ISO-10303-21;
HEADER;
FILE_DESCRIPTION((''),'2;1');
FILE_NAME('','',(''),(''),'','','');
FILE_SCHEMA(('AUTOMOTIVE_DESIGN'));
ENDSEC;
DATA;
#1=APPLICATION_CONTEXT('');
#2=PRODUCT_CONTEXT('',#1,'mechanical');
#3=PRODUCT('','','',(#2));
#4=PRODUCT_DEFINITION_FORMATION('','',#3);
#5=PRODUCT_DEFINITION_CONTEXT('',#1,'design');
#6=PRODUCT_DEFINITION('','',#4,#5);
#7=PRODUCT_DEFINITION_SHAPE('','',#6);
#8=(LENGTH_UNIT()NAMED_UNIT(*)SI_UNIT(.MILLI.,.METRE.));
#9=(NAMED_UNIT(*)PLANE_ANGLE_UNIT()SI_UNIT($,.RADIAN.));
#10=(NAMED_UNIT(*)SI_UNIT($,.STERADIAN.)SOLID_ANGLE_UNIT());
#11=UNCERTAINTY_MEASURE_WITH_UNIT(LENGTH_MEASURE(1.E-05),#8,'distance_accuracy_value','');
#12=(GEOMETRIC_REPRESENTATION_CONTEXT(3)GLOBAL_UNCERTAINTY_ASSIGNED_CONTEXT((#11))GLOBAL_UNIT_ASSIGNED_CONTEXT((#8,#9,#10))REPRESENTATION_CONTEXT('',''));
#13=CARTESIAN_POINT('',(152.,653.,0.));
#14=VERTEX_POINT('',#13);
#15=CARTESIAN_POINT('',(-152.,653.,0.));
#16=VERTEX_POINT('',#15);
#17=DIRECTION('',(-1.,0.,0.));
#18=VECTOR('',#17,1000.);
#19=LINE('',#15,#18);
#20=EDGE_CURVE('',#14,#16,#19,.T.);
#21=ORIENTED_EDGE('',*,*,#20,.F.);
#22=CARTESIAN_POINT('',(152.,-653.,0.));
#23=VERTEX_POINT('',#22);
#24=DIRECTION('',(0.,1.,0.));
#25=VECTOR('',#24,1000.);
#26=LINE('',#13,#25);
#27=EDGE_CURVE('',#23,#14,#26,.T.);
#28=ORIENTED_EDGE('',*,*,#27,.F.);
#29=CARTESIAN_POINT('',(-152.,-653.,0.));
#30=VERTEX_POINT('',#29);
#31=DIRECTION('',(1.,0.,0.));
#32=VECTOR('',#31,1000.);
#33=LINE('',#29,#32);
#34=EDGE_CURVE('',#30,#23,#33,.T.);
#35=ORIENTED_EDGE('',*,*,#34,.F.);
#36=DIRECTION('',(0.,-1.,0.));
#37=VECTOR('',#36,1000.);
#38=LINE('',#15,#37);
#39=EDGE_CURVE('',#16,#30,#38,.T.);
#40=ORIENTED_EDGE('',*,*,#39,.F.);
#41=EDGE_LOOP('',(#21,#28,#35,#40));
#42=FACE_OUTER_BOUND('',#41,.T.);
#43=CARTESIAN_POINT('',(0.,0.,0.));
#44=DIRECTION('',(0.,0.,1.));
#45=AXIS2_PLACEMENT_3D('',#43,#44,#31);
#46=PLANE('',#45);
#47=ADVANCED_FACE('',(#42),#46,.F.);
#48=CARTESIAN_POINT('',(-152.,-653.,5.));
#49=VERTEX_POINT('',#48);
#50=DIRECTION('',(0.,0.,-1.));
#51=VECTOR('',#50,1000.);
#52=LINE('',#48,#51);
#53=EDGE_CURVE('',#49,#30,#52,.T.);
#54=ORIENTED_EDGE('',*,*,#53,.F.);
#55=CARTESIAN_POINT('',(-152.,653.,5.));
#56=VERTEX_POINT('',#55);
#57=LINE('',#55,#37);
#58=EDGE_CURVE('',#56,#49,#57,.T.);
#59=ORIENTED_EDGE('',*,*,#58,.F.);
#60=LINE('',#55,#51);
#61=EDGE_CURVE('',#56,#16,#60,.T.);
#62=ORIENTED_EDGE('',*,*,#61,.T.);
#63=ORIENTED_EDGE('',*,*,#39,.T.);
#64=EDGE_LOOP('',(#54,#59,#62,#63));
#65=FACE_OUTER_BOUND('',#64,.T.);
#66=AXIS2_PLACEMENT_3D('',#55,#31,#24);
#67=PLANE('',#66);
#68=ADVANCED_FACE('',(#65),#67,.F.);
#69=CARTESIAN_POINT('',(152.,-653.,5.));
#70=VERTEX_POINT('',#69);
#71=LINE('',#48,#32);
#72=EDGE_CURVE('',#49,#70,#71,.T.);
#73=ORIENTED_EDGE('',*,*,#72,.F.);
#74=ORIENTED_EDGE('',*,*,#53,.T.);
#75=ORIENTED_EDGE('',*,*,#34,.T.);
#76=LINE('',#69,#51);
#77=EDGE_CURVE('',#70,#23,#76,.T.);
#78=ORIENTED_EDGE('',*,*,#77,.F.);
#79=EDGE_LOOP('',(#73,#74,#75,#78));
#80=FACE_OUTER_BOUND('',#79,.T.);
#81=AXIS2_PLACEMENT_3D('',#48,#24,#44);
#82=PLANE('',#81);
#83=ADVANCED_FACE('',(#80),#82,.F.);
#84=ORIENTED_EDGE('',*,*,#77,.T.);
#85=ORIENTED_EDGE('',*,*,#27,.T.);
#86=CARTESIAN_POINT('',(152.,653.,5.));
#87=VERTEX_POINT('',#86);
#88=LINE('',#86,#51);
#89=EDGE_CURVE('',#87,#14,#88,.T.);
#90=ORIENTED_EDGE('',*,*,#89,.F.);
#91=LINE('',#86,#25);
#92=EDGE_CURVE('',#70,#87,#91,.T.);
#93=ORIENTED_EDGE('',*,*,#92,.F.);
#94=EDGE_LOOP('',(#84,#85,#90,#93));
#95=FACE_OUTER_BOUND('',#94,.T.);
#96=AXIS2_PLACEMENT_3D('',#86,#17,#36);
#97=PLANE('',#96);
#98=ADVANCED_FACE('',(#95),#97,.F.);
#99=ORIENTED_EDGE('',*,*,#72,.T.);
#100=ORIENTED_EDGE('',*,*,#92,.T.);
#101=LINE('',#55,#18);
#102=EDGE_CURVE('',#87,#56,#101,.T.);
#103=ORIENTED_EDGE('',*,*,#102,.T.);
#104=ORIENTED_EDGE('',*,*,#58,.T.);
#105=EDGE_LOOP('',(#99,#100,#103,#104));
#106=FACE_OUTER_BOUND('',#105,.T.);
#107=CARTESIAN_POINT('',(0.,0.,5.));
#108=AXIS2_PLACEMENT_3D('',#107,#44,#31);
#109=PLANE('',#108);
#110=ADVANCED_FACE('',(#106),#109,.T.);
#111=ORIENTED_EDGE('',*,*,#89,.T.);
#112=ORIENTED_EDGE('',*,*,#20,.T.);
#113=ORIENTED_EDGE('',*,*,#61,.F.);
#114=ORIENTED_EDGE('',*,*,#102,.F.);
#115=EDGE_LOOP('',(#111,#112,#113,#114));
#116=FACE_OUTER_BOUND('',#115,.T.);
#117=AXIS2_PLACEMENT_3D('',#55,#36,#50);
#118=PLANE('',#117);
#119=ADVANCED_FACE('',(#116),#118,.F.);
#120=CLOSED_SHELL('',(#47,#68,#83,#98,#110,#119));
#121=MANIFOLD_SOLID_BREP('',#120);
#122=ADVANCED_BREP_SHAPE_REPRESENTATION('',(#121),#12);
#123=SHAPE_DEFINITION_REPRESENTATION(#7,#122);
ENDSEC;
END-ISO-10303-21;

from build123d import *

# Parameters (mm, degrees)
SKETCH_1_W      = 304
SKETCH_1_H      = 1306
EXTRUDE_1_DEPTH = 5


with BuildPart() as part:
    # 草图1 → 凸台-拉伸1 (new body)
    with BuildSketch(Plane.XY):
        Rectangle(SKETCH_1_W, SKETCH_1_H)
    extrude(amount=EXTRUDE_1_DEPTH)


solid = part.part
